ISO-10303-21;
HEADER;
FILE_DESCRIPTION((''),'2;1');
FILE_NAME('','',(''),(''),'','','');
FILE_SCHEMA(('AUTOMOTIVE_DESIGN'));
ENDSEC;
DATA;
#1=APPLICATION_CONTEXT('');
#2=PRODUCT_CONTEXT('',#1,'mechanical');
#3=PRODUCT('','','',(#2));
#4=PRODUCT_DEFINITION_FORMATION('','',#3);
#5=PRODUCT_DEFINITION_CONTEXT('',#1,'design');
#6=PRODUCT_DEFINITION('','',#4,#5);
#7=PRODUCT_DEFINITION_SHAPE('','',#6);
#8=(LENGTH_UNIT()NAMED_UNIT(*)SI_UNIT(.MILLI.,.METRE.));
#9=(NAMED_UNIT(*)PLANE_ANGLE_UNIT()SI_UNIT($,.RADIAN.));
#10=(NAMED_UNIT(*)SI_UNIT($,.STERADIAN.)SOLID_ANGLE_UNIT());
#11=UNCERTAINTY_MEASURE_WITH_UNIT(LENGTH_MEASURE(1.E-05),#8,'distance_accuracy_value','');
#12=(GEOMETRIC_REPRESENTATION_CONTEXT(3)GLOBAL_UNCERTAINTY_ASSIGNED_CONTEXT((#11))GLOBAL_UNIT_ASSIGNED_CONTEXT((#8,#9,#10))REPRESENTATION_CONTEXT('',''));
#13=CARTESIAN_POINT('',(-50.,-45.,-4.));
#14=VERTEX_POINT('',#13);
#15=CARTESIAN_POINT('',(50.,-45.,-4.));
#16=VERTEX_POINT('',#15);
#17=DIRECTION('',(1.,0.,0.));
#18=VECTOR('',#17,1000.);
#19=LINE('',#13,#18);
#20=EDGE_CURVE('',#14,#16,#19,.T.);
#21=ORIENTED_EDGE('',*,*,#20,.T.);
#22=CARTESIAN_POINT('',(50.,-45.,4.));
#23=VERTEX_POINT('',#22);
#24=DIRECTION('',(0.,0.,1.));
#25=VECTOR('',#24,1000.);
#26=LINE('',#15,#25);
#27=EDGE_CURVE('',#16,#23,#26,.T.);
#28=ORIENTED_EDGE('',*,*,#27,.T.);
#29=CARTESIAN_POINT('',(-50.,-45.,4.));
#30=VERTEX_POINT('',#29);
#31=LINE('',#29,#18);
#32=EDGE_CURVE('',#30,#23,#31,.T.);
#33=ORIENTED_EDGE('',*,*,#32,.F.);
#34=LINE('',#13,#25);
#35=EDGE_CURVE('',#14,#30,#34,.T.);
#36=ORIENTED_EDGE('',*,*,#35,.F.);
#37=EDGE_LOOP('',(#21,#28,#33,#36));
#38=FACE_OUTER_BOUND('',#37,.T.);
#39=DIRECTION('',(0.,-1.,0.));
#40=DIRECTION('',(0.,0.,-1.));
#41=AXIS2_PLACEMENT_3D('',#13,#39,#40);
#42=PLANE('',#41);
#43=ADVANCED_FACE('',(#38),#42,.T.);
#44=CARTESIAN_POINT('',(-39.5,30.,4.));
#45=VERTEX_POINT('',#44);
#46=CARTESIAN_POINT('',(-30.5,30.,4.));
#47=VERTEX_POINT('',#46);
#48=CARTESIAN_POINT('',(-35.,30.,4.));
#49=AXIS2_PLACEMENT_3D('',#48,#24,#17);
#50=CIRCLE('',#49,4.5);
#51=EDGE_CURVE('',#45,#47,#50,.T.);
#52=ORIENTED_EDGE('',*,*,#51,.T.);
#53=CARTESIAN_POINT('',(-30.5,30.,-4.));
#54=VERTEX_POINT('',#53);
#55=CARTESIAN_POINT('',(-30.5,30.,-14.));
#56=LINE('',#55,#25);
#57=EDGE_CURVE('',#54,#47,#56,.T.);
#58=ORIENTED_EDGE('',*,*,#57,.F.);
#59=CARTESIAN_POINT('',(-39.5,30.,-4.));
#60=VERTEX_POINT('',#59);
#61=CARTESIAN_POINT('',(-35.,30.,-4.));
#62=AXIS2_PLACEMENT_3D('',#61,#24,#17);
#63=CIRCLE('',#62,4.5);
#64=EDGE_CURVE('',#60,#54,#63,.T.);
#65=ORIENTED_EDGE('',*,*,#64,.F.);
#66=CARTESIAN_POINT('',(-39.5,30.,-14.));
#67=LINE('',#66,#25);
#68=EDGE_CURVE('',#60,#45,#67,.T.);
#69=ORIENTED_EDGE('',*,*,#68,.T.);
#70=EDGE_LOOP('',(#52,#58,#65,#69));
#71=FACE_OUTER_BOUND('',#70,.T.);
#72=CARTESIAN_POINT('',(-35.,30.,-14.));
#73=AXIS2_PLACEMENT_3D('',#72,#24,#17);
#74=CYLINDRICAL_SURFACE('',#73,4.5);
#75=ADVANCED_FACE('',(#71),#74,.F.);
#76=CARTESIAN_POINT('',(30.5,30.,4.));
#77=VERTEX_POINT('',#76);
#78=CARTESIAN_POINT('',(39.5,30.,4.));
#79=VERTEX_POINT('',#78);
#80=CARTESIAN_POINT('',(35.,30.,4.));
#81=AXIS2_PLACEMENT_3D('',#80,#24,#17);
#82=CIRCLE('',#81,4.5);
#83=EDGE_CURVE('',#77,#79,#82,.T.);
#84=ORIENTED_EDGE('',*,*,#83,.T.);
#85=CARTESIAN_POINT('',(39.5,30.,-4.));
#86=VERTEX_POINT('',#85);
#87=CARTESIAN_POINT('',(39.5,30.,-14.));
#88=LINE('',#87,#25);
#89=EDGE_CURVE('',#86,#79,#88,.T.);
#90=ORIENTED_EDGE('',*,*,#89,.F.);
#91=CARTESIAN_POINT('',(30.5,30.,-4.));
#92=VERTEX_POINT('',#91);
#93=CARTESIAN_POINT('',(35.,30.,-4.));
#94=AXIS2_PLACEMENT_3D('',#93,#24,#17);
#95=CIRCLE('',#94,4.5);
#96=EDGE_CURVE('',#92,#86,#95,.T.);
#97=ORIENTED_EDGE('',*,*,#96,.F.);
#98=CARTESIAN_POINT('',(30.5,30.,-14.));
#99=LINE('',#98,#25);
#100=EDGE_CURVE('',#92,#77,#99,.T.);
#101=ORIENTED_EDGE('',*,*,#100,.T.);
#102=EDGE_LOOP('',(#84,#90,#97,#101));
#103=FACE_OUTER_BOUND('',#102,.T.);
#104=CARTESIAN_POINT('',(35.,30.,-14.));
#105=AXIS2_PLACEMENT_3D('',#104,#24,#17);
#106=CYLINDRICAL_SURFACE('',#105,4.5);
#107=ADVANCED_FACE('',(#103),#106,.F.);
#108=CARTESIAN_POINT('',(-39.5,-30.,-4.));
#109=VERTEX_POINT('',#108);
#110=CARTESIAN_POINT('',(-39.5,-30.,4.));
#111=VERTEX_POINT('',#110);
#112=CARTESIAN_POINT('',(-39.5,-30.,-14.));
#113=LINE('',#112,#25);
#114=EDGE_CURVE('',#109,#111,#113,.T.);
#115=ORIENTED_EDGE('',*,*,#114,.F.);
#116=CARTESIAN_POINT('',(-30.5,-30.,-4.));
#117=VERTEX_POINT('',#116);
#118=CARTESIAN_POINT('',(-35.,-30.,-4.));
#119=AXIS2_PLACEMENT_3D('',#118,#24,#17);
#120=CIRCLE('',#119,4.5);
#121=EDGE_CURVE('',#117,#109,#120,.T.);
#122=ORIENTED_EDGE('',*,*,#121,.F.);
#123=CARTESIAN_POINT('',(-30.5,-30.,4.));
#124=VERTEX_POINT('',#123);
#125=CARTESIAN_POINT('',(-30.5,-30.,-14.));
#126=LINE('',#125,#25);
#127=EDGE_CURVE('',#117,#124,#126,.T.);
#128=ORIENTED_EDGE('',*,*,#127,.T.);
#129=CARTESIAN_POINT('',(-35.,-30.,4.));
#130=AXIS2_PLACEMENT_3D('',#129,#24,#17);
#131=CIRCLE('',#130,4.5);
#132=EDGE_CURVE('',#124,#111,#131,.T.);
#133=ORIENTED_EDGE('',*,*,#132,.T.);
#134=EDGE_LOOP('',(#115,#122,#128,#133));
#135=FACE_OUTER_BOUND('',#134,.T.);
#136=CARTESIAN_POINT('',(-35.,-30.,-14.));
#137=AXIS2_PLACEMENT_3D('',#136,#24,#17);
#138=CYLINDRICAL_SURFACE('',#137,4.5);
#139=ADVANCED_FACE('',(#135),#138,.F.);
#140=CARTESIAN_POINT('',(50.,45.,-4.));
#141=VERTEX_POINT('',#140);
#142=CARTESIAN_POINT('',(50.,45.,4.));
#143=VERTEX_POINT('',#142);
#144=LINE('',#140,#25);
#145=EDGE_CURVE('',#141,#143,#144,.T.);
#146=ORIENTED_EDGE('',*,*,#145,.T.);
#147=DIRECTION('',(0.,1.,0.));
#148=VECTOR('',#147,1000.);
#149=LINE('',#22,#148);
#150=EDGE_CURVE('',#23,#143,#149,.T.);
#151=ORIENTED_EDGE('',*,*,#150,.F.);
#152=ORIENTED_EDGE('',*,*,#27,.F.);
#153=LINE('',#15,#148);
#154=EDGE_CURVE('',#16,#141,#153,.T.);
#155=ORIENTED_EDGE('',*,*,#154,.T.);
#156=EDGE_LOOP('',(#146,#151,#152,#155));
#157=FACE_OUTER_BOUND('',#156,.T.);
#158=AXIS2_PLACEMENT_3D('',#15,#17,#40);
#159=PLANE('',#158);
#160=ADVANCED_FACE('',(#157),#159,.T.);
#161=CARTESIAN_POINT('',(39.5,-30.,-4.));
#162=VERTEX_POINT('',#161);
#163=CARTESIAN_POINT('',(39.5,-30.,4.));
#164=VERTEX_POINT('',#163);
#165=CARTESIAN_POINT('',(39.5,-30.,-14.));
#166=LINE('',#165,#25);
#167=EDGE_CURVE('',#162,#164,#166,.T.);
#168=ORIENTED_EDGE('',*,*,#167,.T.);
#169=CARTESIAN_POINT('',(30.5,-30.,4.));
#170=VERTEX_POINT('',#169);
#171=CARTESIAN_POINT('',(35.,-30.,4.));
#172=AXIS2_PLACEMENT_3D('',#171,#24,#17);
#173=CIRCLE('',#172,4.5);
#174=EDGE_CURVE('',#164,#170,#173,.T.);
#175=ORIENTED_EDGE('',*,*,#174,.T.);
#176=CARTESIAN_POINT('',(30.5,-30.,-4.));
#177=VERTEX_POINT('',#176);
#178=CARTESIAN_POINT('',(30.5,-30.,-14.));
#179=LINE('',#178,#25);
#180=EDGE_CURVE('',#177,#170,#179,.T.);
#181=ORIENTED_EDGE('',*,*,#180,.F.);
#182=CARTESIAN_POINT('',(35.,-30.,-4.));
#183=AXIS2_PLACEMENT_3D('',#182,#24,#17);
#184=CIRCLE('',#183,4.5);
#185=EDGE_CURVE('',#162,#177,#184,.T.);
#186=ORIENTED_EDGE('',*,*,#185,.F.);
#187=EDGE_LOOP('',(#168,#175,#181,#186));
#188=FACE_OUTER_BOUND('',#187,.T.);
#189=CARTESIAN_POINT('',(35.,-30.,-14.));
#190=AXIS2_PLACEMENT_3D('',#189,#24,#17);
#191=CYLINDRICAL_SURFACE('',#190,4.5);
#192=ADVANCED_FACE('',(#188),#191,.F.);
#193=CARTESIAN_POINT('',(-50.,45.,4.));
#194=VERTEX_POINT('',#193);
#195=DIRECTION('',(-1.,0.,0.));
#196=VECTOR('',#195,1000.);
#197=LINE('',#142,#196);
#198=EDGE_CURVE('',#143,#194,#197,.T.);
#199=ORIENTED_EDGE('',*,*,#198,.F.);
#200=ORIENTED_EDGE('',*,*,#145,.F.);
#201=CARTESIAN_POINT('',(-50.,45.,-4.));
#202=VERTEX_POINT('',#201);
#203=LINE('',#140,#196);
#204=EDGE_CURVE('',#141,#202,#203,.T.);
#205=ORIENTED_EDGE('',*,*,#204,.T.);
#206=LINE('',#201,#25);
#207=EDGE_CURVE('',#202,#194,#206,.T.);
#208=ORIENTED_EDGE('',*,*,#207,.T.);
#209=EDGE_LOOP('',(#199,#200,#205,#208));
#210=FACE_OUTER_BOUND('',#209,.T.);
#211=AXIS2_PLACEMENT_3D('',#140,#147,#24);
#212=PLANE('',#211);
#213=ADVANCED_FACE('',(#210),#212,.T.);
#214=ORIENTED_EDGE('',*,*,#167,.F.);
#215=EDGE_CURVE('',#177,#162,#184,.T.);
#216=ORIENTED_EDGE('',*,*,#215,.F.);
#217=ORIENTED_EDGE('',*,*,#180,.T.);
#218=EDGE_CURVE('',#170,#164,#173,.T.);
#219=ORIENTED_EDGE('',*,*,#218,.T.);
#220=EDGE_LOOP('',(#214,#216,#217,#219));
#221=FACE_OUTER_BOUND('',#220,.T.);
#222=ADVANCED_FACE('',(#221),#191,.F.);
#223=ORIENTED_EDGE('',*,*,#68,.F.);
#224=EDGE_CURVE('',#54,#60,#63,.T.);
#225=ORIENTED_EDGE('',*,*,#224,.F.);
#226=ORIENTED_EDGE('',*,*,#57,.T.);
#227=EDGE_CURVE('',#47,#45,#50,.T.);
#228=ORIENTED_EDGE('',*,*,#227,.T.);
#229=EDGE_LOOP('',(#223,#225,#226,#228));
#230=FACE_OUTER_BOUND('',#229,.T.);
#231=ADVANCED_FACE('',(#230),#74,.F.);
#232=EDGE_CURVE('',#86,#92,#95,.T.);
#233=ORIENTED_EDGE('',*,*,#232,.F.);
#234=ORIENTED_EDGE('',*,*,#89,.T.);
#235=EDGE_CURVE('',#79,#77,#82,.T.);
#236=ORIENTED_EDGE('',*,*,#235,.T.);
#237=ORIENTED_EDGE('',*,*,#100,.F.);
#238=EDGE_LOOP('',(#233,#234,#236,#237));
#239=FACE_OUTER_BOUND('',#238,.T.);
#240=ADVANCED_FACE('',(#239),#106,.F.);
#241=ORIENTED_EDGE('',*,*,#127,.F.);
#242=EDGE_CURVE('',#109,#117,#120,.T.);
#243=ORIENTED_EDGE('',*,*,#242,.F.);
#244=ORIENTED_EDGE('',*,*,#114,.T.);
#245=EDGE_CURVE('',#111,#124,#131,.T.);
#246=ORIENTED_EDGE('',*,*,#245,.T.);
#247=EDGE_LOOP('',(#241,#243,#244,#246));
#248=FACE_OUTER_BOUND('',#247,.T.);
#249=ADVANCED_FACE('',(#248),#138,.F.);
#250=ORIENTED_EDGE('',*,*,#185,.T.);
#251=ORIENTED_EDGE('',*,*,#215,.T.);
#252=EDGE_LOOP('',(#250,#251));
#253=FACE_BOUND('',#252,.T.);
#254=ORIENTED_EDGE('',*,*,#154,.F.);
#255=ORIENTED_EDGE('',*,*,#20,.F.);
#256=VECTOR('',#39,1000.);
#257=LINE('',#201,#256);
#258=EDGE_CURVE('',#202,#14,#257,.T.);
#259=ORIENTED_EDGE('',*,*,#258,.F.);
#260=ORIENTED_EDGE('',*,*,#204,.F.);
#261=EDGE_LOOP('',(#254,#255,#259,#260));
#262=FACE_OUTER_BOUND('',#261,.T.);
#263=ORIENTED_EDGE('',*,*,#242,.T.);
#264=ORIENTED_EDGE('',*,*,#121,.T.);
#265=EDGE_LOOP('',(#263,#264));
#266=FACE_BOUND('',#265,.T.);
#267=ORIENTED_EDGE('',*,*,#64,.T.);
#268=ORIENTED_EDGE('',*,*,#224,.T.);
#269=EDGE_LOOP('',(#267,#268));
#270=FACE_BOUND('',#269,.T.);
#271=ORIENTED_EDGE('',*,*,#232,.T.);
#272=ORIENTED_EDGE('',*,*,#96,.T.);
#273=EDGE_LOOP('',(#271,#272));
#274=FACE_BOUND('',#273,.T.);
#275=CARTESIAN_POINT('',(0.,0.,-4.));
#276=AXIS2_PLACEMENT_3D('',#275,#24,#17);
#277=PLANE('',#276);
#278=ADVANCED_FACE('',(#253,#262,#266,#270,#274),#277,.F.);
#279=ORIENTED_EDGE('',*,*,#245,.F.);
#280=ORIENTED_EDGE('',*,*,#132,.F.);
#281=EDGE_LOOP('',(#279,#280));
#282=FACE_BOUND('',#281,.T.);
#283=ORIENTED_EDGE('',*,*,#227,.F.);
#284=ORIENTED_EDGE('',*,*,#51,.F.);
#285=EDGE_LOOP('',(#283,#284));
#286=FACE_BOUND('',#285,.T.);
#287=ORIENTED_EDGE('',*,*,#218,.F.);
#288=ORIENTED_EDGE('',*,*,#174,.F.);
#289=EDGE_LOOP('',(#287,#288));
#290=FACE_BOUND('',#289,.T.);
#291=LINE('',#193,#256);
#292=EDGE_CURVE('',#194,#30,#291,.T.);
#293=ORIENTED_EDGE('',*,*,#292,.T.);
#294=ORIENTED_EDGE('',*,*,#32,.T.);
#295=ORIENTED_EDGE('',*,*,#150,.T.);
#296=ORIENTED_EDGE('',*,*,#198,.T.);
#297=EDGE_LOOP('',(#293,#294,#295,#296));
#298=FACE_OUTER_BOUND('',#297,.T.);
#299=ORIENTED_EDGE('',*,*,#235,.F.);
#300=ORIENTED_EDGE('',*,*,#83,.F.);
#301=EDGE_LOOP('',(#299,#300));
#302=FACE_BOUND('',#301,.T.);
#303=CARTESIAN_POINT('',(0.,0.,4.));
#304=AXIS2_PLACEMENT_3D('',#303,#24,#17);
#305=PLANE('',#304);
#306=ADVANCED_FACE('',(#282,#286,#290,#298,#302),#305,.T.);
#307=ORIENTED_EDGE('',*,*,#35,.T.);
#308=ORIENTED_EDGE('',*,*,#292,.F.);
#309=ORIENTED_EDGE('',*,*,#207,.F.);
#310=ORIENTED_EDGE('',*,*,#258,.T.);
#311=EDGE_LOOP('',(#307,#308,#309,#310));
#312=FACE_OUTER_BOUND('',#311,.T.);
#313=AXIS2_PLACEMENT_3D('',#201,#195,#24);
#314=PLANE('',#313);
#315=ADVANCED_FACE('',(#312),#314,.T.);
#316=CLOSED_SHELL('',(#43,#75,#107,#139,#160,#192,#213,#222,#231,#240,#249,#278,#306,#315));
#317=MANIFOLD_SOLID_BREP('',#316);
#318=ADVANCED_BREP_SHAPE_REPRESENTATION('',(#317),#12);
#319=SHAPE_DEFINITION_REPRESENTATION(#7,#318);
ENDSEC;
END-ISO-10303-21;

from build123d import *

# Parameters (mm, degrees)
SKETCH_1_W          = 100
SKETCH_1_H          = 90
EXTRUDE_1_DEPTH     = 4
SKETCH_2_R          = 4.5
CUT_EXTRUDE_1_DEPTH = 14


with BuildPart() as part:
    # 草图1 → 凸台-拉伸1 (new, symmetric)
    with BuildSketch(Plane.XY):
        Rectangle(SKETCH_1_W, SKETCH_1_H)
    extrude(amount=EXTRUDE_1_DEPTH, both=True)

    # 草图2 → 切除-拉伸1 (cut, symmetric)
    with BuildSketch(Plane.XY):
        with Locations((-35, -30)):
            Circle(SKETCH_2_R)
        with Locations((35, -30)):
            Circle(SKETCH_2_R)
        with Locations((-35, 30)):
            Circle(SKETCH_2_R)
        with Locations((35, 30)):
            Circle(SKETCH_2_R)
    extrude(amount=CUT_EXTRUDE_1_DEPTH, both=True, mode=Mode.SUBTRACT)


solid = part.part
